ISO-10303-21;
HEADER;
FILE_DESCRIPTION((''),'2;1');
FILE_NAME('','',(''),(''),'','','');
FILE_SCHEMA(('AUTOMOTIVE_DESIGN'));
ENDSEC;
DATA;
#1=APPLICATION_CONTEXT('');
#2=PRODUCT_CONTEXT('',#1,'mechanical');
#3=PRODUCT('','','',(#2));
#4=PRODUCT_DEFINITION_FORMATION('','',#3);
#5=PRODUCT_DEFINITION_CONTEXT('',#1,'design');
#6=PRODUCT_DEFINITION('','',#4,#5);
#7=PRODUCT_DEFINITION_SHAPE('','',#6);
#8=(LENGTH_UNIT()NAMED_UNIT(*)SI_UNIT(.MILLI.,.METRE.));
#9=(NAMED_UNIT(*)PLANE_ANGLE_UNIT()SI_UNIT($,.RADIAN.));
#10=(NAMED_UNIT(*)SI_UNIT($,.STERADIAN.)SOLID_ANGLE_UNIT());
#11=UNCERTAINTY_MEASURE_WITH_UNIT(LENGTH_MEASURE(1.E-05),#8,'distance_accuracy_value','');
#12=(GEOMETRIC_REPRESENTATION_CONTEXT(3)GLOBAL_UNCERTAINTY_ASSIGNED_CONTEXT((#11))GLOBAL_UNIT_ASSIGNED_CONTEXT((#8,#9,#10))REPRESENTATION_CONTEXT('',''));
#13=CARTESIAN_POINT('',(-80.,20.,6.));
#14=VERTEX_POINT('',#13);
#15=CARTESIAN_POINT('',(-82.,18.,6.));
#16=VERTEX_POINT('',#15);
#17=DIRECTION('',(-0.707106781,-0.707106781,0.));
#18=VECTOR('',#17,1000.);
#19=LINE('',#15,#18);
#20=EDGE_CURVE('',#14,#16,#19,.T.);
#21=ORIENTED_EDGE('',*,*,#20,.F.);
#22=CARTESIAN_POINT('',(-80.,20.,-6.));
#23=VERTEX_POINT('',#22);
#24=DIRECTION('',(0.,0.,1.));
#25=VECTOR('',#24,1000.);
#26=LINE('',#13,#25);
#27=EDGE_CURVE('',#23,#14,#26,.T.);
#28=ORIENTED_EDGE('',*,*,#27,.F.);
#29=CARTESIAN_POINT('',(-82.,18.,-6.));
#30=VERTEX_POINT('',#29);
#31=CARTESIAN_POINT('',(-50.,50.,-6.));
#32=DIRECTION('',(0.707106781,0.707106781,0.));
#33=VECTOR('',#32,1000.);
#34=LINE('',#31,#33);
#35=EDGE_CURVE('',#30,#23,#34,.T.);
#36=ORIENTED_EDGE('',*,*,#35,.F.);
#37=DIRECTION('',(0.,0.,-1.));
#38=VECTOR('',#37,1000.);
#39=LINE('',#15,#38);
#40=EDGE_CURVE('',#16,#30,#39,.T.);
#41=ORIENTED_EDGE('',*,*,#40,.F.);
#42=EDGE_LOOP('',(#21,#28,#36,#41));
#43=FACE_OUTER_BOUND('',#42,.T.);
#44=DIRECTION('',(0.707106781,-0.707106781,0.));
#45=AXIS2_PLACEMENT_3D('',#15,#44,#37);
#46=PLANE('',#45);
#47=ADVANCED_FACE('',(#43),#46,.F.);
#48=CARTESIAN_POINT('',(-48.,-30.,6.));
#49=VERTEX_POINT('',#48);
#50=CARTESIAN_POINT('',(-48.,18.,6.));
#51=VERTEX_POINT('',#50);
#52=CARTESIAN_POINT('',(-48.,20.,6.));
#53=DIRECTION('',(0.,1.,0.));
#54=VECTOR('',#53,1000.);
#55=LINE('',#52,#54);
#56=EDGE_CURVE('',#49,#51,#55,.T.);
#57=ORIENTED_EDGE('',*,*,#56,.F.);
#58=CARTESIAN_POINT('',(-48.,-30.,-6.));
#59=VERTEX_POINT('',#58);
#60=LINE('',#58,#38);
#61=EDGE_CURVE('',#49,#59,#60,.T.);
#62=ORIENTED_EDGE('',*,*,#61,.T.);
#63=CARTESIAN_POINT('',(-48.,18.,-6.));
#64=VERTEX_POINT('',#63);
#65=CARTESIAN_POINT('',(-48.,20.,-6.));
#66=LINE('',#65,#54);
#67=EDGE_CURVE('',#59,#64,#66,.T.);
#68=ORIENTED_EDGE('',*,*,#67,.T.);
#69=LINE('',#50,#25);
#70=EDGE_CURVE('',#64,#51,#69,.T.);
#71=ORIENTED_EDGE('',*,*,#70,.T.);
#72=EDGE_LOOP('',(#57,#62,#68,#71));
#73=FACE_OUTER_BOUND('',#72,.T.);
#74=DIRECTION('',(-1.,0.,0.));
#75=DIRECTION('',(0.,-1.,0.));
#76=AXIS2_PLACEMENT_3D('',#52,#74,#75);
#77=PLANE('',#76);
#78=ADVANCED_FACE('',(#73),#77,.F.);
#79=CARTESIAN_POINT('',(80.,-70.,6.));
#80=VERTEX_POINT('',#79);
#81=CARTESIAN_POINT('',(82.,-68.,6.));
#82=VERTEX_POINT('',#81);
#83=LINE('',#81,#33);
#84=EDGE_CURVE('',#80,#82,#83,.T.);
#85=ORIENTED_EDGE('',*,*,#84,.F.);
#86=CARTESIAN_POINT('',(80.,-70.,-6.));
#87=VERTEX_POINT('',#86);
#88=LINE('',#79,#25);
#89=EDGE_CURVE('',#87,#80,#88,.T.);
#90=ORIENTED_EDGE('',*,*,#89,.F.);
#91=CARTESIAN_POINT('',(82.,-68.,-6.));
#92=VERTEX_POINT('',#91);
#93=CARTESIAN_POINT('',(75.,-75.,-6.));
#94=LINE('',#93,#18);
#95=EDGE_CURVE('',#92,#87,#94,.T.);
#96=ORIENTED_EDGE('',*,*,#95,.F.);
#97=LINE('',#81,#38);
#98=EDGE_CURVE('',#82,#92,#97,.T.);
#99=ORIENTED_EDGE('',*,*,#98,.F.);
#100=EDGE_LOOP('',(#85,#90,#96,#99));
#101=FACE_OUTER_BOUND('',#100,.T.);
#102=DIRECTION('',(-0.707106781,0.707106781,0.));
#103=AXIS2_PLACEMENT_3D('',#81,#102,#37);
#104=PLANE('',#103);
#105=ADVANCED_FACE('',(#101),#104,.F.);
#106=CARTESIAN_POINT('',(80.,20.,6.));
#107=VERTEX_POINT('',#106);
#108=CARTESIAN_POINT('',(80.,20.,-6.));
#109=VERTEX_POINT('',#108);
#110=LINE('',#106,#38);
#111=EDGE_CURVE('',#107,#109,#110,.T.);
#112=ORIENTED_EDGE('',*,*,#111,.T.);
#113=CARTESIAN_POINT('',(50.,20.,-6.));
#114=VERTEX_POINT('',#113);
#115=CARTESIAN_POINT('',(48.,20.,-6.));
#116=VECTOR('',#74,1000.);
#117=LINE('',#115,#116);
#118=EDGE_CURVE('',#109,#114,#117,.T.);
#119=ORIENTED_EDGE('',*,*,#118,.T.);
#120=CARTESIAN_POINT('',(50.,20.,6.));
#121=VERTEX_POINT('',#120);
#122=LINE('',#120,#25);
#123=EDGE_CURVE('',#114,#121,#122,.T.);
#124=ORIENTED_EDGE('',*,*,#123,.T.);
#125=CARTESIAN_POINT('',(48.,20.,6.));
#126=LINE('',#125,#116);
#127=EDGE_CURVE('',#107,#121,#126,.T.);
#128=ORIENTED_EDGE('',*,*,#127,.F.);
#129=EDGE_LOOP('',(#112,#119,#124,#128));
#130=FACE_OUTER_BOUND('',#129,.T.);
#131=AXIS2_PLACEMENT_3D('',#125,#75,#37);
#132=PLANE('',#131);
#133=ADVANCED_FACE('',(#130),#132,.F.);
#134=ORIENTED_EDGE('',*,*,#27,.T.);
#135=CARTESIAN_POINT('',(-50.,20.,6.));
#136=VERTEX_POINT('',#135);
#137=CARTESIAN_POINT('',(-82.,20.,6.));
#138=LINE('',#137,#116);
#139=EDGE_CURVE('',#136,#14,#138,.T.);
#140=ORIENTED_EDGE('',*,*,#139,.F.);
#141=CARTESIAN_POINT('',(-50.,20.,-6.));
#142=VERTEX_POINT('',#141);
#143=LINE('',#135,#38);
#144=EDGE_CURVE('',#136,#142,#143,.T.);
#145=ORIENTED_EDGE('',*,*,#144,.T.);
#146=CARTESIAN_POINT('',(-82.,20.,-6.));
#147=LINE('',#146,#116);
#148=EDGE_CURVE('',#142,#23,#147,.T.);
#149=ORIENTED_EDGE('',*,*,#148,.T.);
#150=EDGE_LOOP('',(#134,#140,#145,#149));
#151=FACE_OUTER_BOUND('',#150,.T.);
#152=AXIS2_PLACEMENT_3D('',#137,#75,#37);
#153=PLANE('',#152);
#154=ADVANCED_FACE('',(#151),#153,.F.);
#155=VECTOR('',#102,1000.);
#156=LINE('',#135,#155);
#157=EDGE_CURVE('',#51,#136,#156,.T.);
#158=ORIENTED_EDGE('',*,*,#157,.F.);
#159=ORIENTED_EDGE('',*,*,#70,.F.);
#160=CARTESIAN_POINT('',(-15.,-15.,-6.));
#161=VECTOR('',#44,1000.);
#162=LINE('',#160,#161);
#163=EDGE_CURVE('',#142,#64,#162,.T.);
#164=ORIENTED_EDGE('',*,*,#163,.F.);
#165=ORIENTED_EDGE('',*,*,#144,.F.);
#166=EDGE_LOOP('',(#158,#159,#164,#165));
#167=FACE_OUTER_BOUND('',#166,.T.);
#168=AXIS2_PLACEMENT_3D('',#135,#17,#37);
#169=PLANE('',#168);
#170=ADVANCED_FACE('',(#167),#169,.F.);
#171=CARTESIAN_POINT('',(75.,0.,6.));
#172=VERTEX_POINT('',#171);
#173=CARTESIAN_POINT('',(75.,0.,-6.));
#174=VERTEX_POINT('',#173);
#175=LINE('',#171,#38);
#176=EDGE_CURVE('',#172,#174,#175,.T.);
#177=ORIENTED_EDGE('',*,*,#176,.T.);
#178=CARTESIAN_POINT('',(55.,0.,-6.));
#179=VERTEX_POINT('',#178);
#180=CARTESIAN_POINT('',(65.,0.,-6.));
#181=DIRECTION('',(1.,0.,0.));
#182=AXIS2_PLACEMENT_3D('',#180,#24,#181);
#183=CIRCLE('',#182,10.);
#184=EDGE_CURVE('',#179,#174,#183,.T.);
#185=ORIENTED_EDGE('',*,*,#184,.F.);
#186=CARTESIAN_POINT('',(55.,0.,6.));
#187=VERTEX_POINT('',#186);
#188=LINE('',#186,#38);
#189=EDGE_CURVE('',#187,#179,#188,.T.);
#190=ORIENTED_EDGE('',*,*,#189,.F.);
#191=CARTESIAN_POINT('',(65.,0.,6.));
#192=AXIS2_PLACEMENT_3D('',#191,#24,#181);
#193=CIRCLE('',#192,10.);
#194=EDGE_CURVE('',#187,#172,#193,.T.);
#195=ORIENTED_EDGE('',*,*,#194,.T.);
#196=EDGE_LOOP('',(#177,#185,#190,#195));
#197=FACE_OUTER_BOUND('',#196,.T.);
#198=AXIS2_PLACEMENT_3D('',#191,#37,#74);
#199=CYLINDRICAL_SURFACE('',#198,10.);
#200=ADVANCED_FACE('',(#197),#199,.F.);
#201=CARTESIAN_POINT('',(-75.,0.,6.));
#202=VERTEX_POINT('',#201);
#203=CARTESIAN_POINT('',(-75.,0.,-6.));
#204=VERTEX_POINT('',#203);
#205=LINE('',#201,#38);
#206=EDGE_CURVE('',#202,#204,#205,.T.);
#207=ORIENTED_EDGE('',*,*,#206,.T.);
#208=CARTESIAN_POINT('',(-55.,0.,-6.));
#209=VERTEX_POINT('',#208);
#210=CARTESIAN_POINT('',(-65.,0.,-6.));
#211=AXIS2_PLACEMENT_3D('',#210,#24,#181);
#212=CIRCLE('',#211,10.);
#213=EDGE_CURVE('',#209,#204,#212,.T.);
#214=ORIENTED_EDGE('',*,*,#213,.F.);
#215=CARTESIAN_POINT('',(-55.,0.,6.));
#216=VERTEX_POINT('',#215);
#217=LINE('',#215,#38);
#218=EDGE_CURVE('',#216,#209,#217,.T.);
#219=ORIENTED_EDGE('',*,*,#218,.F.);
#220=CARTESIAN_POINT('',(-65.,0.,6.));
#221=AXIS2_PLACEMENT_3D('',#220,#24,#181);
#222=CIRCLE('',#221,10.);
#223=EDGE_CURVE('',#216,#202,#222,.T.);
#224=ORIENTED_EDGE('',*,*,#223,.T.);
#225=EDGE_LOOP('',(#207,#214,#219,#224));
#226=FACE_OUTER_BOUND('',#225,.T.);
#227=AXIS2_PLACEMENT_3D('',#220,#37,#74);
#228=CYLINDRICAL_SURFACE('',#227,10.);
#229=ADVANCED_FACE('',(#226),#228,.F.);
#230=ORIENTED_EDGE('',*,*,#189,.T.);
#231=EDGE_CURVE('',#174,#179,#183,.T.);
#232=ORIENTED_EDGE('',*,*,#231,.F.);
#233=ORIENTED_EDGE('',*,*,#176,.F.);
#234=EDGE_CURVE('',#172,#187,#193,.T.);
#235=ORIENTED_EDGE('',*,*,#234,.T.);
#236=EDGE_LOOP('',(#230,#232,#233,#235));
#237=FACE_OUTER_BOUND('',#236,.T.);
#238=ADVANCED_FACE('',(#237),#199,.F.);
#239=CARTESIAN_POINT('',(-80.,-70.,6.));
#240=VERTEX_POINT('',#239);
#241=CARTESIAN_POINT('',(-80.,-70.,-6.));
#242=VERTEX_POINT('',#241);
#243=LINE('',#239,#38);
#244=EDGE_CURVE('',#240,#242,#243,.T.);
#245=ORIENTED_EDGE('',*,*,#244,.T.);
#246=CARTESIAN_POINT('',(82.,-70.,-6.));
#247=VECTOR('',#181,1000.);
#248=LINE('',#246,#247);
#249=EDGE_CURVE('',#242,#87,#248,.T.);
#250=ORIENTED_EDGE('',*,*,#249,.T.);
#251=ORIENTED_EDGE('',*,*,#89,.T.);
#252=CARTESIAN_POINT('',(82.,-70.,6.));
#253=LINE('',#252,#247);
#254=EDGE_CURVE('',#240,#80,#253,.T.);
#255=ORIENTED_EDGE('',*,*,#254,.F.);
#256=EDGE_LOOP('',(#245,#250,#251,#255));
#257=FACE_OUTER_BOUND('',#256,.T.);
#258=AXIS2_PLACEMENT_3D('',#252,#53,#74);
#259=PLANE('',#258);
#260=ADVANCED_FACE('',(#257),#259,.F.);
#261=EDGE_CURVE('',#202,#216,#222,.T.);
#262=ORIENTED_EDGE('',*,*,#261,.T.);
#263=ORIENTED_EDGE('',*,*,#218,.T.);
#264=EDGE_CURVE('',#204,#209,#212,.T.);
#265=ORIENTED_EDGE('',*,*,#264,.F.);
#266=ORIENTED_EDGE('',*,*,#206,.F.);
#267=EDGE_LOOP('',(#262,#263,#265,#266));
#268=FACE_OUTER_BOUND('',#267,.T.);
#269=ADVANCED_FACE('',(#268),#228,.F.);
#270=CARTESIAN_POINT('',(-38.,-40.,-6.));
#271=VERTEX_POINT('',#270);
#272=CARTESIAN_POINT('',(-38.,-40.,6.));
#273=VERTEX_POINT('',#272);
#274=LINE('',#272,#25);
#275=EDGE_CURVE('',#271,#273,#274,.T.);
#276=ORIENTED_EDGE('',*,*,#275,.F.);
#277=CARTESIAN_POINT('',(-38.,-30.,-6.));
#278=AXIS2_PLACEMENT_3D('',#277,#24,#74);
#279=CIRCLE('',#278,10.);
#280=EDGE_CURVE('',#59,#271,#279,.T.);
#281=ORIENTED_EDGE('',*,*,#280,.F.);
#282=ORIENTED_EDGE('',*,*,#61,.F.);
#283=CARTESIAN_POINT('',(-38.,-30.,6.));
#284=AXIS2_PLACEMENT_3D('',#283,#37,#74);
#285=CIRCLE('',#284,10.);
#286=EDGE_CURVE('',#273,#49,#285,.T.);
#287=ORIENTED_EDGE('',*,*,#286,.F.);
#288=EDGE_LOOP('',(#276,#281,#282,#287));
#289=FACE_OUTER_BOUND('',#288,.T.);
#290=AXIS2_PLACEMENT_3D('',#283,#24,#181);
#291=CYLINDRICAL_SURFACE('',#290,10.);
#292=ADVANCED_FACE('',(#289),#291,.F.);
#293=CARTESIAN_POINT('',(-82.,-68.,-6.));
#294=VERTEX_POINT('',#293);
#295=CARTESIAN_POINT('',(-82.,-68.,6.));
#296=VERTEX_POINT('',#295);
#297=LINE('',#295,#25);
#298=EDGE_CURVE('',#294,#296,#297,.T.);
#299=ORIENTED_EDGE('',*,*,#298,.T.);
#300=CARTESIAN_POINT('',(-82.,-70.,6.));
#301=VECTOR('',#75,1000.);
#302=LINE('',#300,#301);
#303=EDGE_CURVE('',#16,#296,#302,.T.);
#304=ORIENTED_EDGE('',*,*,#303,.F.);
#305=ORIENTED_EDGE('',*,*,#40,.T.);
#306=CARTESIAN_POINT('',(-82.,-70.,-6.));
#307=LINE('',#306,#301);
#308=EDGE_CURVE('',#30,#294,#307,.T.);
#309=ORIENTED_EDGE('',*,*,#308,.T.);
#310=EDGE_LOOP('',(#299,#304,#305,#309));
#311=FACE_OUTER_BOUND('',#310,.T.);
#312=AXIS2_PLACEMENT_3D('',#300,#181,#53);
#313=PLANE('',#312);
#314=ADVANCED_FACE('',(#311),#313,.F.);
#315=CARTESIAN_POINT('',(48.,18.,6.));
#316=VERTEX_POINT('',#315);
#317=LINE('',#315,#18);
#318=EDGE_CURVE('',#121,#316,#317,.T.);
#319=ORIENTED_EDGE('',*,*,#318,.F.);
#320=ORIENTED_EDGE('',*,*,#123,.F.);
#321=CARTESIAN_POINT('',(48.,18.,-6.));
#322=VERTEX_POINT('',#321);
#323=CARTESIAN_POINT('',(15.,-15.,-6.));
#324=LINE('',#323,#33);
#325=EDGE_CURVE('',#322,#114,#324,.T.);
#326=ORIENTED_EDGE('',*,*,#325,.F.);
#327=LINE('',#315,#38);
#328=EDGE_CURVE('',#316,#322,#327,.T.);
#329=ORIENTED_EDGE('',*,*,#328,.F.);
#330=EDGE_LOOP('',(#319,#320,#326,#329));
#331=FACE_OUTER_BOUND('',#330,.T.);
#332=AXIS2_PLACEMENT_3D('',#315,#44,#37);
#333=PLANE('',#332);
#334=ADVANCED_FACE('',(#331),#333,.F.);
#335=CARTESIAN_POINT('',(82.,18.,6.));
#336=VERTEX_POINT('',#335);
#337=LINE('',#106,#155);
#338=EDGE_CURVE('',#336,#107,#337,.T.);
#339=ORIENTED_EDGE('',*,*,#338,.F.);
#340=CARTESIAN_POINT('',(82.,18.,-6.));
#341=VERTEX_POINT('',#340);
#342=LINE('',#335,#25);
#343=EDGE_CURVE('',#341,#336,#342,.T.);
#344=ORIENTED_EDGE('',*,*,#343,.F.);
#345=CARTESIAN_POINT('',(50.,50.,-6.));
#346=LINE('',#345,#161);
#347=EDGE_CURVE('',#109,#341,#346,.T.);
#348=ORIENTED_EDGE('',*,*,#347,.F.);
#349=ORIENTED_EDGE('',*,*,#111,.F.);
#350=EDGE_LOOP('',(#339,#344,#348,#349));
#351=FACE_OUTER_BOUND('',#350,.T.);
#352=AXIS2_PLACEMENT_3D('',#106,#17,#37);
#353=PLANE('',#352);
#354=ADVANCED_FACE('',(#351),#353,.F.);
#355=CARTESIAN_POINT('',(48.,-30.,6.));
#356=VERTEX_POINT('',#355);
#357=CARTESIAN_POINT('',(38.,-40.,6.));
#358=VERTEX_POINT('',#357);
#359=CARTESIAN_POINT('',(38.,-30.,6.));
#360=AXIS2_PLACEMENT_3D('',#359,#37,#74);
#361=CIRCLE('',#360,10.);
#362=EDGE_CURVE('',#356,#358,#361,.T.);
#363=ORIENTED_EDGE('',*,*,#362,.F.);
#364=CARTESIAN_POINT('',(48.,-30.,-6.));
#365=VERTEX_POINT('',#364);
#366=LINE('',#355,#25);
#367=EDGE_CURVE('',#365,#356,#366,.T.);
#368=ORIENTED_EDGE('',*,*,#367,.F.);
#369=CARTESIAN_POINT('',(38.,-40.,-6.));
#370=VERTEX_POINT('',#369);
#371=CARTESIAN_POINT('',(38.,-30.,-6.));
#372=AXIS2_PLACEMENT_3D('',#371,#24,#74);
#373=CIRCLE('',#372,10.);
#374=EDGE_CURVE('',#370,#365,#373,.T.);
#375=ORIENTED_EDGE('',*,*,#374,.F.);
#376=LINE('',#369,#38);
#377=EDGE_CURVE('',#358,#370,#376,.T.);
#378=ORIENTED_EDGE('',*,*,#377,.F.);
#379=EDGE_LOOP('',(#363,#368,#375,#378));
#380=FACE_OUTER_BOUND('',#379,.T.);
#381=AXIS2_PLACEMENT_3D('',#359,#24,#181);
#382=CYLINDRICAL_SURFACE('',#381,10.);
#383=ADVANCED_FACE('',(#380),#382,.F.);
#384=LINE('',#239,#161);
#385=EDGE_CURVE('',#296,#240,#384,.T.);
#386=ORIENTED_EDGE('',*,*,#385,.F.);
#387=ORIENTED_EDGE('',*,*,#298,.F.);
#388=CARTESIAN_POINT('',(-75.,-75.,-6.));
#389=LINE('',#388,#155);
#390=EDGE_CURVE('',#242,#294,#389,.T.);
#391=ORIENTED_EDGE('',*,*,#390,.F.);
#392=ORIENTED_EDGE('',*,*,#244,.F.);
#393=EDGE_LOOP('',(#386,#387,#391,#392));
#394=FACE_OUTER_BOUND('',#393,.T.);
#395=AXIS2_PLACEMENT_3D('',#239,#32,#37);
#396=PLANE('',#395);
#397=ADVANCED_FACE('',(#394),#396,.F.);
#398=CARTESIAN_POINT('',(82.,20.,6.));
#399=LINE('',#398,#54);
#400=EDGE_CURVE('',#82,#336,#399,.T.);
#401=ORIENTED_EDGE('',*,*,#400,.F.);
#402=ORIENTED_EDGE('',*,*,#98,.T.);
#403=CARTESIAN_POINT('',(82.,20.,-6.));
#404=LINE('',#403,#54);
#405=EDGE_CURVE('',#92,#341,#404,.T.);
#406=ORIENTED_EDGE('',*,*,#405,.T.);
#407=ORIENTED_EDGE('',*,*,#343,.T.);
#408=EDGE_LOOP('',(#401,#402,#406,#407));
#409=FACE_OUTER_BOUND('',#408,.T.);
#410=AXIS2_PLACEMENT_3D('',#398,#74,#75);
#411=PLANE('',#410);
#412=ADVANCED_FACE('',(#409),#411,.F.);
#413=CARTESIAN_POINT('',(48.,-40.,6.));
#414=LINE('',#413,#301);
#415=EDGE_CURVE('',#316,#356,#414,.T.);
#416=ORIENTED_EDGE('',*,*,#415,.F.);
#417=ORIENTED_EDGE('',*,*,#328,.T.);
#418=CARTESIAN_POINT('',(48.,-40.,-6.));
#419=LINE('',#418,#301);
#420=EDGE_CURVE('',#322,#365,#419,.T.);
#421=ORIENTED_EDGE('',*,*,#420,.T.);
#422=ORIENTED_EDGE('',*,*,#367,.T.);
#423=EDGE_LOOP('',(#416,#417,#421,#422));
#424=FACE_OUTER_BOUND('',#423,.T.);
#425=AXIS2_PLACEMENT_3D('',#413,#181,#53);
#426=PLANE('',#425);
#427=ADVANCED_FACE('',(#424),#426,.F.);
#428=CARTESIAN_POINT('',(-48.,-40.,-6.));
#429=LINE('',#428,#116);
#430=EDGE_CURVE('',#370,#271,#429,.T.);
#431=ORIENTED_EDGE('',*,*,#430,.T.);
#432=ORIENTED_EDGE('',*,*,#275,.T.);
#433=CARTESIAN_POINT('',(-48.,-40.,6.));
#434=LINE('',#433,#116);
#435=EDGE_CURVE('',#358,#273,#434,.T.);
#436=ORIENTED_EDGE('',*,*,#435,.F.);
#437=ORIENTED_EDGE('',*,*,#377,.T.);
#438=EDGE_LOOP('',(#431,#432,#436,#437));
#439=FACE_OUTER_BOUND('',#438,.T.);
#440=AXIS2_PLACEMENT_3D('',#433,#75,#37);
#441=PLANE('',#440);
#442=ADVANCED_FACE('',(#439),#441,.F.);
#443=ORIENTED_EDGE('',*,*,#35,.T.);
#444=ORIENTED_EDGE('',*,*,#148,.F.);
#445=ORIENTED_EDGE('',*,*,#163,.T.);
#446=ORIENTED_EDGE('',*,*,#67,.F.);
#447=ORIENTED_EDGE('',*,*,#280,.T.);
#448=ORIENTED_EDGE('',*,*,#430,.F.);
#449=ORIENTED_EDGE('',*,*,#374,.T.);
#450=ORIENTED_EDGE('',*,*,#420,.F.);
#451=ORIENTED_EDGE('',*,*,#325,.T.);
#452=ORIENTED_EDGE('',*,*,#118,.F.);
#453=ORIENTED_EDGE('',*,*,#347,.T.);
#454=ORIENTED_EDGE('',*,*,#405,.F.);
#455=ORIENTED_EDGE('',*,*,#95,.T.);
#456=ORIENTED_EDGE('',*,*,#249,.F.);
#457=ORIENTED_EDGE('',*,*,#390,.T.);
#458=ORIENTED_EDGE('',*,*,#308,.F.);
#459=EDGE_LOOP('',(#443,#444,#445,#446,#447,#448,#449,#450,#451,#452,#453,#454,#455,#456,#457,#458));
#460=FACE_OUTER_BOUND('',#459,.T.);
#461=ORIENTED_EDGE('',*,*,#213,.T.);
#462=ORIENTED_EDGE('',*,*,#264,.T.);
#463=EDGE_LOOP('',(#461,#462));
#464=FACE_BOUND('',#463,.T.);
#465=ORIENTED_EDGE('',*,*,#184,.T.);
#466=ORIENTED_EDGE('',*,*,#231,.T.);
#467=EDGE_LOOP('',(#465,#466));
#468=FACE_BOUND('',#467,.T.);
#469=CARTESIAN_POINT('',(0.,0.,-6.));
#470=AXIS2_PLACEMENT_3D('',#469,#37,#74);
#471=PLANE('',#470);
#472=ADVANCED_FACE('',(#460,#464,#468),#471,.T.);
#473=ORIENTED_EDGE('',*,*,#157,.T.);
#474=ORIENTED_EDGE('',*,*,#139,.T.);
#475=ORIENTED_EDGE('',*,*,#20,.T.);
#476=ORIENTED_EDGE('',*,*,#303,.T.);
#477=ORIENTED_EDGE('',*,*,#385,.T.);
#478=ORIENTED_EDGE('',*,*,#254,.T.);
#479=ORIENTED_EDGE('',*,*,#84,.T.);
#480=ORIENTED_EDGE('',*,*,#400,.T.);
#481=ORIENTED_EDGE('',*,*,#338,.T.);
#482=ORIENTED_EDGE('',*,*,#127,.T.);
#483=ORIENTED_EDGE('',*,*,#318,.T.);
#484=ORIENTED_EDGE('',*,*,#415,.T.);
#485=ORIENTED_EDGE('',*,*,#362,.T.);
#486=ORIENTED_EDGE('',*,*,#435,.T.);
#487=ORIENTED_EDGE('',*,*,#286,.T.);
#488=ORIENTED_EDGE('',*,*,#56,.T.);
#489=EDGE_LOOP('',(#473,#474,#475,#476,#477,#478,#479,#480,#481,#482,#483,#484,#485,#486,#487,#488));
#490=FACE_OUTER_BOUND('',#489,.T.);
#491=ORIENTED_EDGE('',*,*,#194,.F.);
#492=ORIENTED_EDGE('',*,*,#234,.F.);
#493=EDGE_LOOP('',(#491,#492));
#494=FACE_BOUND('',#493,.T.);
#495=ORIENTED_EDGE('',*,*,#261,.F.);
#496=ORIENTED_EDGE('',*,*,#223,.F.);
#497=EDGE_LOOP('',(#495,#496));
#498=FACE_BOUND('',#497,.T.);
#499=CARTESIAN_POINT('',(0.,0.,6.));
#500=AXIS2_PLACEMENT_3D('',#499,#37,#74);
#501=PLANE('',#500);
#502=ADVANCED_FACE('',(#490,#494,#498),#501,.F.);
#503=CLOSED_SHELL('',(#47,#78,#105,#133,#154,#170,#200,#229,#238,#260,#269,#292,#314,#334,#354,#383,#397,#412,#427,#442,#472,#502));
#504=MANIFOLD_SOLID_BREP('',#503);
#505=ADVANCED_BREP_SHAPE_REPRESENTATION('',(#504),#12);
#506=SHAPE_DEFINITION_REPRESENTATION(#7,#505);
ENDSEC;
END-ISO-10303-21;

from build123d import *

# Parameters (mm, degrees)
SKETCH_1_R      = 10
EXTRUDE_1_DEPTH = 6
FILLET_1_R      = 10
CHAMFER_1_SIZE  = 2


with BuildPart() as part:
    # 草图1 → 凸台-拉伸1 (new, symmetric)
    with BuildSketch(Plane.XY):
        Polygon((-82, -70), (-82, 20), (-48, 20), (-48, -40), (48, -40), (48, 20), (82, 20), (82, -70), align=None)
        with Locations((-65, 0)):
            Circle(SKETCH_1_R, mode=Mode.SUBTRACT)
        with Locations((65, 0)):
            Circle(SKETCH_1_R, mode=Mode.SUBTRACT)
    extrude(amount=EXTRUDE_1_DEPTH, both=True)

    # 圆角1
    fillet_1_edges = [part.edges().sort_by_distance(p)[0] for p in [
        (-48, -40, 0),
        (48, -40, 0),
    ]]
    fillet(fillet_1_edges, radius=FILLET_1_R)

    # 倒角1
    chamfer_1_edges = [part.edges().sort_by_distance(p)[0] for p in [
        (-48, 20, 0),
        (48, 20, 0),
        (82, 20, 0),
        (82, -70, 0),
        (-82, -70, 0),
        (-82, 20, 0),
    ]]
    chamfer(chamfer_1_edges, length=CHAMFER_1_SIZE)


solid = part.part
